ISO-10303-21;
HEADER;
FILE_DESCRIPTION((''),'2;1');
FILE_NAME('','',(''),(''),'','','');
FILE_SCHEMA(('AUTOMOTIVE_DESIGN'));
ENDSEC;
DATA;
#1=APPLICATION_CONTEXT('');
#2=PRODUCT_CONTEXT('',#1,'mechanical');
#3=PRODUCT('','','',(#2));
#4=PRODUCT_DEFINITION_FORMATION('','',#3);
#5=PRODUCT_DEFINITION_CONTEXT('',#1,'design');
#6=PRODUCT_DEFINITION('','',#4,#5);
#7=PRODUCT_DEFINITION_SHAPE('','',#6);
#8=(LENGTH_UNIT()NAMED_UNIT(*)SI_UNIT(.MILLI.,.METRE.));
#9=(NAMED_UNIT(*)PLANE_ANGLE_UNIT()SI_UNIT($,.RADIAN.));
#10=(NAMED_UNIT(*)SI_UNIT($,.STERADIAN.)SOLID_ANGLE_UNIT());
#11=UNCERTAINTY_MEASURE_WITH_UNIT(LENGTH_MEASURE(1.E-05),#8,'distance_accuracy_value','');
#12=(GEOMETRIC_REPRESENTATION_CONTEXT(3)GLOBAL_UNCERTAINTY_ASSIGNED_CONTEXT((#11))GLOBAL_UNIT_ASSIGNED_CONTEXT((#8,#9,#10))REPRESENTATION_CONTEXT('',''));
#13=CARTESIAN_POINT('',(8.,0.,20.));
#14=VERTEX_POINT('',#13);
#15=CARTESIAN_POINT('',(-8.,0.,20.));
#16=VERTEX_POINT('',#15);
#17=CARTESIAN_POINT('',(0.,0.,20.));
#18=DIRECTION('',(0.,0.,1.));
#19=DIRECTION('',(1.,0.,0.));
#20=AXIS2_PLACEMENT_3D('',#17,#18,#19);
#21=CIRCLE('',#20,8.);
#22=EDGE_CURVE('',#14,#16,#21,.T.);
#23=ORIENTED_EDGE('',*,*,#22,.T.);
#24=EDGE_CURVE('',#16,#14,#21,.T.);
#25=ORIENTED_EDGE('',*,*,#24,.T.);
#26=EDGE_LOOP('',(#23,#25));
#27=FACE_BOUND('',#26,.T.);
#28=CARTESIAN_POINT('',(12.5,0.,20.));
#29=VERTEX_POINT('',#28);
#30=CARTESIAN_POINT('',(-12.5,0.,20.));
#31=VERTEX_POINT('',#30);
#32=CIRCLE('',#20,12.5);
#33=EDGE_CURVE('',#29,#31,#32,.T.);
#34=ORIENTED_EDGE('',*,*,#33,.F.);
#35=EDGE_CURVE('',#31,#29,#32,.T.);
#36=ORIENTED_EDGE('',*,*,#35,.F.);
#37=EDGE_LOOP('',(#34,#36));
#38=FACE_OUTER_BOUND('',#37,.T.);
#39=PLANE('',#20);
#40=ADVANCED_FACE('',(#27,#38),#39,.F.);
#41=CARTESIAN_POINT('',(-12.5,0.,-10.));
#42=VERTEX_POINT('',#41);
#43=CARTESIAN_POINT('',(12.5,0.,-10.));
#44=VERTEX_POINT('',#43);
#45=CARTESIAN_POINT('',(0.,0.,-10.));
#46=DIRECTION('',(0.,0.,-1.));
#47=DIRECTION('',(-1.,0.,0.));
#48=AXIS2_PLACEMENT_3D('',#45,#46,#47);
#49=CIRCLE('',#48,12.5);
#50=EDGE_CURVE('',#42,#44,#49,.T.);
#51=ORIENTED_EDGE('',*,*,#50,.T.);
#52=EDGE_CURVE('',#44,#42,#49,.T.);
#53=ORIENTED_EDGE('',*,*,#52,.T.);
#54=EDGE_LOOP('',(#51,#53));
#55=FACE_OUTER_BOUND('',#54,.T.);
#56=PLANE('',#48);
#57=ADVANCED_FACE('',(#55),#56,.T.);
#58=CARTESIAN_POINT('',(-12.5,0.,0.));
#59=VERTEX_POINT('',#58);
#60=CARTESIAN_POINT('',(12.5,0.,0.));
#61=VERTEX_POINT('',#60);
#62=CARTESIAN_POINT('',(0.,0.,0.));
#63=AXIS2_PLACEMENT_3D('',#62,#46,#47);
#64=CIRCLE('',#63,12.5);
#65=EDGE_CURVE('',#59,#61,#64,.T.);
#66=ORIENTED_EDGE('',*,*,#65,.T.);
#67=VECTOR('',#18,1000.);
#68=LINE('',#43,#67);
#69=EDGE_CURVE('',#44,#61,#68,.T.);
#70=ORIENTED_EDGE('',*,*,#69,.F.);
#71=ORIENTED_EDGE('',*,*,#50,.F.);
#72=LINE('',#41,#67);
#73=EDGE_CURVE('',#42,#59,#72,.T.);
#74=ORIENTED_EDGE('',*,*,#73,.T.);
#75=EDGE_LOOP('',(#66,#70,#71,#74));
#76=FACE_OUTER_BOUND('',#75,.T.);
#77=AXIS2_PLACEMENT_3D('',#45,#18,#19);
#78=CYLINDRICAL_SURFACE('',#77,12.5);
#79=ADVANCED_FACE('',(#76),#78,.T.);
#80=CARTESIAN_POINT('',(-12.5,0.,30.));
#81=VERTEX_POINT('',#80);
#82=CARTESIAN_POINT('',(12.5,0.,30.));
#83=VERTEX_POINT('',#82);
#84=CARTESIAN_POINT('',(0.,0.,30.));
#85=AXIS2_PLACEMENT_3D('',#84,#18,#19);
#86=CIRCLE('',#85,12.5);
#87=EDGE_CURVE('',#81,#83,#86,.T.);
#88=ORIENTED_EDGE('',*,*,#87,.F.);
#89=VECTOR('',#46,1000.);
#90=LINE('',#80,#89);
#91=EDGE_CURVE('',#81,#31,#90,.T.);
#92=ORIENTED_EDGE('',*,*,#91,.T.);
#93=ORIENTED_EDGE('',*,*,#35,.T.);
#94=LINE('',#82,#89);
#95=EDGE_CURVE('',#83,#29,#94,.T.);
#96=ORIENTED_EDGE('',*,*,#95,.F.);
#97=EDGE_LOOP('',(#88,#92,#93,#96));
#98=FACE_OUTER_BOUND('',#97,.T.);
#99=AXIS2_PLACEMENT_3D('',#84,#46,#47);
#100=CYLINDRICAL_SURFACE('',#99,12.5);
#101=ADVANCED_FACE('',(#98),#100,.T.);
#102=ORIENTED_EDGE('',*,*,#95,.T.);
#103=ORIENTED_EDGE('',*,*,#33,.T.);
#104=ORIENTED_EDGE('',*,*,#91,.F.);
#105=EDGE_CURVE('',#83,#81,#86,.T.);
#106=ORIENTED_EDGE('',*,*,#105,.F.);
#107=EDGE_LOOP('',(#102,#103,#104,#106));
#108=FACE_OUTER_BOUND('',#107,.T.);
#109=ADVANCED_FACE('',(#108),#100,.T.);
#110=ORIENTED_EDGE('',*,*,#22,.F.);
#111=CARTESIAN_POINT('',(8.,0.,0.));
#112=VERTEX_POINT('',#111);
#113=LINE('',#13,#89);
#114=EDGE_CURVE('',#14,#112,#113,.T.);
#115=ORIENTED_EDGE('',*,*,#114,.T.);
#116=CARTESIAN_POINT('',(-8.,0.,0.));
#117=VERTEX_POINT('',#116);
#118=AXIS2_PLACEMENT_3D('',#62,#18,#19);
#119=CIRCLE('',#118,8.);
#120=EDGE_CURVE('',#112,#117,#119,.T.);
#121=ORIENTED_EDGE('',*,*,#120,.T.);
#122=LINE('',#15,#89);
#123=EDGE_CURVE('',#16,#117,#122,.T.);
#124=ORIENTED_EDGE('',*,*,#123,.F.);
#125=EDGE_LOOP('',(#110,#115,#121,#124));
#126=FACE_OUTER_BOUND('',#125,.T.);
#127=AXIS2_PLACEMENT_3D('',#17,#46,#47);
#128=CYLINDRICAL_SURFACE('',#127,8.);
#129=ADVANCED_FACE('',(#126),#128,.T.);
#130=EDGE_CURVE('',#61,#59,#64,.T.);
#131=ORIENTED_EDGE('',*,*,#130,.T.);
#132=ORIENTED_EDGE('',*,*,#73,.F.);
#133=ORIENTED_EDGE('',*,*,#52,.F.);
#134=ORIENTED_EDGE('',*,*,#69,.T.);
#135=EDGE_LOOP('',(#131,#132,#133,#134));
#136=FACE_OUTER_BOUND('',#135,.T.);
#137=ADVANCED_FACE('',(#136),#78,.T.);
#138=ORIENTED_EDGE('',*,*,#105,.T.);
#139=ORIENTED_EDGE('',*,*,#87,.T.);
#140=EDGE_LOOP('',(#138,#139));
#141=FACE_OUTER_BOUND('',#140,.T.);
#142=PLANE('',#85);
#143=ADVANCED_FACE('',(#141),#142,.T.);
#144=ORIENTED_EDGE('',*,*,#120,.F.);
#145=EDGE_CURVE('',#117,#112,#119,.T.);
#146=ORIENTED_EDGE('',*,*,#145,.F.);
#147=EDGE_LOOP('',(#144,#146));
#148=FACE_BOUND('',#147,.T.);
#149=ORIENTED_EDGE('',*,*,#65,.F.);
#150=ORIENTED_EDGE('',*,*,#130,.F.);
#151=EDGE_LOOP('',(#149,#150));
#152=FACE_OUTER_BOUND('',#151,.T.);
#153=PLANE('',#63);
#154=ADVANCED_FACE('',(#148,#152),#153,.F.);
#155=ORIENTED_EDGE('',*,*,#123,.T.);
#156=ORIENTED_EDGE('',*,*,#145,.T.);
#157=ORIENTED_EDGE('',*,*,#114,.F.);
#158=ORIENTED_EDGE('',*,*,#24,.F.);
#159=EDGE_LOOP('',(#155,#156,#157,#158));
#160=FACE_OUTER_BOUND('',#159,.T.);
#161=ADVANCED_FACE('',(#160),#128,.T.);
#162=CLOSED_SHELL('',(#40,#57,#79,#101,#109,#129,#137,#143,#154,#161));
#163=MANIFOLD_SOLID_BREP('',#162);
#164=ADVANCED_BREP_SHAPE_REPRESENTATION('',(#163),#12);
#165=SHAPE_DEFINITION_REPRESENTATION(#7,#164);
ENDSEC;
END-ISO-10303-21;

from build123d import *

# Parameters (mm, degrees)
SKETCH1_R           = 8
BOSS_EXTRUDE1_DEPTH = 20
SKETCH2_R           = 12.5
BOSS_EXTRUDE2_DEPTH = 10
BOSS_EXTRUDE3_START = 10
SKETCH3_R           = 12.5
BOSS_EXTRUDE3_DEPTH = 10


with BuildPart() as part:
    # Sketch1 → Boss-Extrude1 (new body)
    with BuildSketch(Plane.XY):
        Circle(SKETCH1_R)
    extrude(amount=BOSS_EXTRUDE1_DEPTH)

    # Sketch2 → Boss-Extrude2 (add)
    with BuildSketch(Plane.XY.offset(20)):
        Circle(SKETCH2_R)
    extrude(amount=BOSS_EXTRUDE2_DEPTH)

    # Sketch3 → Boss-Extrude3 (add)
    with BuildSketch(Plane(origin=(0, 0, 0), x_dir=(-1, 0, 0), z_dir=(0, 0, -1)).offset(BOSS_EXTRUDE3_START)):
        with Locations(Location((0, 0, 0), (0, 0, 180))):
            Circle(SKETCH3_R)
    extrude(amount=-BOSS_EXTRUDE3_DEPTH)


solid = part.part
